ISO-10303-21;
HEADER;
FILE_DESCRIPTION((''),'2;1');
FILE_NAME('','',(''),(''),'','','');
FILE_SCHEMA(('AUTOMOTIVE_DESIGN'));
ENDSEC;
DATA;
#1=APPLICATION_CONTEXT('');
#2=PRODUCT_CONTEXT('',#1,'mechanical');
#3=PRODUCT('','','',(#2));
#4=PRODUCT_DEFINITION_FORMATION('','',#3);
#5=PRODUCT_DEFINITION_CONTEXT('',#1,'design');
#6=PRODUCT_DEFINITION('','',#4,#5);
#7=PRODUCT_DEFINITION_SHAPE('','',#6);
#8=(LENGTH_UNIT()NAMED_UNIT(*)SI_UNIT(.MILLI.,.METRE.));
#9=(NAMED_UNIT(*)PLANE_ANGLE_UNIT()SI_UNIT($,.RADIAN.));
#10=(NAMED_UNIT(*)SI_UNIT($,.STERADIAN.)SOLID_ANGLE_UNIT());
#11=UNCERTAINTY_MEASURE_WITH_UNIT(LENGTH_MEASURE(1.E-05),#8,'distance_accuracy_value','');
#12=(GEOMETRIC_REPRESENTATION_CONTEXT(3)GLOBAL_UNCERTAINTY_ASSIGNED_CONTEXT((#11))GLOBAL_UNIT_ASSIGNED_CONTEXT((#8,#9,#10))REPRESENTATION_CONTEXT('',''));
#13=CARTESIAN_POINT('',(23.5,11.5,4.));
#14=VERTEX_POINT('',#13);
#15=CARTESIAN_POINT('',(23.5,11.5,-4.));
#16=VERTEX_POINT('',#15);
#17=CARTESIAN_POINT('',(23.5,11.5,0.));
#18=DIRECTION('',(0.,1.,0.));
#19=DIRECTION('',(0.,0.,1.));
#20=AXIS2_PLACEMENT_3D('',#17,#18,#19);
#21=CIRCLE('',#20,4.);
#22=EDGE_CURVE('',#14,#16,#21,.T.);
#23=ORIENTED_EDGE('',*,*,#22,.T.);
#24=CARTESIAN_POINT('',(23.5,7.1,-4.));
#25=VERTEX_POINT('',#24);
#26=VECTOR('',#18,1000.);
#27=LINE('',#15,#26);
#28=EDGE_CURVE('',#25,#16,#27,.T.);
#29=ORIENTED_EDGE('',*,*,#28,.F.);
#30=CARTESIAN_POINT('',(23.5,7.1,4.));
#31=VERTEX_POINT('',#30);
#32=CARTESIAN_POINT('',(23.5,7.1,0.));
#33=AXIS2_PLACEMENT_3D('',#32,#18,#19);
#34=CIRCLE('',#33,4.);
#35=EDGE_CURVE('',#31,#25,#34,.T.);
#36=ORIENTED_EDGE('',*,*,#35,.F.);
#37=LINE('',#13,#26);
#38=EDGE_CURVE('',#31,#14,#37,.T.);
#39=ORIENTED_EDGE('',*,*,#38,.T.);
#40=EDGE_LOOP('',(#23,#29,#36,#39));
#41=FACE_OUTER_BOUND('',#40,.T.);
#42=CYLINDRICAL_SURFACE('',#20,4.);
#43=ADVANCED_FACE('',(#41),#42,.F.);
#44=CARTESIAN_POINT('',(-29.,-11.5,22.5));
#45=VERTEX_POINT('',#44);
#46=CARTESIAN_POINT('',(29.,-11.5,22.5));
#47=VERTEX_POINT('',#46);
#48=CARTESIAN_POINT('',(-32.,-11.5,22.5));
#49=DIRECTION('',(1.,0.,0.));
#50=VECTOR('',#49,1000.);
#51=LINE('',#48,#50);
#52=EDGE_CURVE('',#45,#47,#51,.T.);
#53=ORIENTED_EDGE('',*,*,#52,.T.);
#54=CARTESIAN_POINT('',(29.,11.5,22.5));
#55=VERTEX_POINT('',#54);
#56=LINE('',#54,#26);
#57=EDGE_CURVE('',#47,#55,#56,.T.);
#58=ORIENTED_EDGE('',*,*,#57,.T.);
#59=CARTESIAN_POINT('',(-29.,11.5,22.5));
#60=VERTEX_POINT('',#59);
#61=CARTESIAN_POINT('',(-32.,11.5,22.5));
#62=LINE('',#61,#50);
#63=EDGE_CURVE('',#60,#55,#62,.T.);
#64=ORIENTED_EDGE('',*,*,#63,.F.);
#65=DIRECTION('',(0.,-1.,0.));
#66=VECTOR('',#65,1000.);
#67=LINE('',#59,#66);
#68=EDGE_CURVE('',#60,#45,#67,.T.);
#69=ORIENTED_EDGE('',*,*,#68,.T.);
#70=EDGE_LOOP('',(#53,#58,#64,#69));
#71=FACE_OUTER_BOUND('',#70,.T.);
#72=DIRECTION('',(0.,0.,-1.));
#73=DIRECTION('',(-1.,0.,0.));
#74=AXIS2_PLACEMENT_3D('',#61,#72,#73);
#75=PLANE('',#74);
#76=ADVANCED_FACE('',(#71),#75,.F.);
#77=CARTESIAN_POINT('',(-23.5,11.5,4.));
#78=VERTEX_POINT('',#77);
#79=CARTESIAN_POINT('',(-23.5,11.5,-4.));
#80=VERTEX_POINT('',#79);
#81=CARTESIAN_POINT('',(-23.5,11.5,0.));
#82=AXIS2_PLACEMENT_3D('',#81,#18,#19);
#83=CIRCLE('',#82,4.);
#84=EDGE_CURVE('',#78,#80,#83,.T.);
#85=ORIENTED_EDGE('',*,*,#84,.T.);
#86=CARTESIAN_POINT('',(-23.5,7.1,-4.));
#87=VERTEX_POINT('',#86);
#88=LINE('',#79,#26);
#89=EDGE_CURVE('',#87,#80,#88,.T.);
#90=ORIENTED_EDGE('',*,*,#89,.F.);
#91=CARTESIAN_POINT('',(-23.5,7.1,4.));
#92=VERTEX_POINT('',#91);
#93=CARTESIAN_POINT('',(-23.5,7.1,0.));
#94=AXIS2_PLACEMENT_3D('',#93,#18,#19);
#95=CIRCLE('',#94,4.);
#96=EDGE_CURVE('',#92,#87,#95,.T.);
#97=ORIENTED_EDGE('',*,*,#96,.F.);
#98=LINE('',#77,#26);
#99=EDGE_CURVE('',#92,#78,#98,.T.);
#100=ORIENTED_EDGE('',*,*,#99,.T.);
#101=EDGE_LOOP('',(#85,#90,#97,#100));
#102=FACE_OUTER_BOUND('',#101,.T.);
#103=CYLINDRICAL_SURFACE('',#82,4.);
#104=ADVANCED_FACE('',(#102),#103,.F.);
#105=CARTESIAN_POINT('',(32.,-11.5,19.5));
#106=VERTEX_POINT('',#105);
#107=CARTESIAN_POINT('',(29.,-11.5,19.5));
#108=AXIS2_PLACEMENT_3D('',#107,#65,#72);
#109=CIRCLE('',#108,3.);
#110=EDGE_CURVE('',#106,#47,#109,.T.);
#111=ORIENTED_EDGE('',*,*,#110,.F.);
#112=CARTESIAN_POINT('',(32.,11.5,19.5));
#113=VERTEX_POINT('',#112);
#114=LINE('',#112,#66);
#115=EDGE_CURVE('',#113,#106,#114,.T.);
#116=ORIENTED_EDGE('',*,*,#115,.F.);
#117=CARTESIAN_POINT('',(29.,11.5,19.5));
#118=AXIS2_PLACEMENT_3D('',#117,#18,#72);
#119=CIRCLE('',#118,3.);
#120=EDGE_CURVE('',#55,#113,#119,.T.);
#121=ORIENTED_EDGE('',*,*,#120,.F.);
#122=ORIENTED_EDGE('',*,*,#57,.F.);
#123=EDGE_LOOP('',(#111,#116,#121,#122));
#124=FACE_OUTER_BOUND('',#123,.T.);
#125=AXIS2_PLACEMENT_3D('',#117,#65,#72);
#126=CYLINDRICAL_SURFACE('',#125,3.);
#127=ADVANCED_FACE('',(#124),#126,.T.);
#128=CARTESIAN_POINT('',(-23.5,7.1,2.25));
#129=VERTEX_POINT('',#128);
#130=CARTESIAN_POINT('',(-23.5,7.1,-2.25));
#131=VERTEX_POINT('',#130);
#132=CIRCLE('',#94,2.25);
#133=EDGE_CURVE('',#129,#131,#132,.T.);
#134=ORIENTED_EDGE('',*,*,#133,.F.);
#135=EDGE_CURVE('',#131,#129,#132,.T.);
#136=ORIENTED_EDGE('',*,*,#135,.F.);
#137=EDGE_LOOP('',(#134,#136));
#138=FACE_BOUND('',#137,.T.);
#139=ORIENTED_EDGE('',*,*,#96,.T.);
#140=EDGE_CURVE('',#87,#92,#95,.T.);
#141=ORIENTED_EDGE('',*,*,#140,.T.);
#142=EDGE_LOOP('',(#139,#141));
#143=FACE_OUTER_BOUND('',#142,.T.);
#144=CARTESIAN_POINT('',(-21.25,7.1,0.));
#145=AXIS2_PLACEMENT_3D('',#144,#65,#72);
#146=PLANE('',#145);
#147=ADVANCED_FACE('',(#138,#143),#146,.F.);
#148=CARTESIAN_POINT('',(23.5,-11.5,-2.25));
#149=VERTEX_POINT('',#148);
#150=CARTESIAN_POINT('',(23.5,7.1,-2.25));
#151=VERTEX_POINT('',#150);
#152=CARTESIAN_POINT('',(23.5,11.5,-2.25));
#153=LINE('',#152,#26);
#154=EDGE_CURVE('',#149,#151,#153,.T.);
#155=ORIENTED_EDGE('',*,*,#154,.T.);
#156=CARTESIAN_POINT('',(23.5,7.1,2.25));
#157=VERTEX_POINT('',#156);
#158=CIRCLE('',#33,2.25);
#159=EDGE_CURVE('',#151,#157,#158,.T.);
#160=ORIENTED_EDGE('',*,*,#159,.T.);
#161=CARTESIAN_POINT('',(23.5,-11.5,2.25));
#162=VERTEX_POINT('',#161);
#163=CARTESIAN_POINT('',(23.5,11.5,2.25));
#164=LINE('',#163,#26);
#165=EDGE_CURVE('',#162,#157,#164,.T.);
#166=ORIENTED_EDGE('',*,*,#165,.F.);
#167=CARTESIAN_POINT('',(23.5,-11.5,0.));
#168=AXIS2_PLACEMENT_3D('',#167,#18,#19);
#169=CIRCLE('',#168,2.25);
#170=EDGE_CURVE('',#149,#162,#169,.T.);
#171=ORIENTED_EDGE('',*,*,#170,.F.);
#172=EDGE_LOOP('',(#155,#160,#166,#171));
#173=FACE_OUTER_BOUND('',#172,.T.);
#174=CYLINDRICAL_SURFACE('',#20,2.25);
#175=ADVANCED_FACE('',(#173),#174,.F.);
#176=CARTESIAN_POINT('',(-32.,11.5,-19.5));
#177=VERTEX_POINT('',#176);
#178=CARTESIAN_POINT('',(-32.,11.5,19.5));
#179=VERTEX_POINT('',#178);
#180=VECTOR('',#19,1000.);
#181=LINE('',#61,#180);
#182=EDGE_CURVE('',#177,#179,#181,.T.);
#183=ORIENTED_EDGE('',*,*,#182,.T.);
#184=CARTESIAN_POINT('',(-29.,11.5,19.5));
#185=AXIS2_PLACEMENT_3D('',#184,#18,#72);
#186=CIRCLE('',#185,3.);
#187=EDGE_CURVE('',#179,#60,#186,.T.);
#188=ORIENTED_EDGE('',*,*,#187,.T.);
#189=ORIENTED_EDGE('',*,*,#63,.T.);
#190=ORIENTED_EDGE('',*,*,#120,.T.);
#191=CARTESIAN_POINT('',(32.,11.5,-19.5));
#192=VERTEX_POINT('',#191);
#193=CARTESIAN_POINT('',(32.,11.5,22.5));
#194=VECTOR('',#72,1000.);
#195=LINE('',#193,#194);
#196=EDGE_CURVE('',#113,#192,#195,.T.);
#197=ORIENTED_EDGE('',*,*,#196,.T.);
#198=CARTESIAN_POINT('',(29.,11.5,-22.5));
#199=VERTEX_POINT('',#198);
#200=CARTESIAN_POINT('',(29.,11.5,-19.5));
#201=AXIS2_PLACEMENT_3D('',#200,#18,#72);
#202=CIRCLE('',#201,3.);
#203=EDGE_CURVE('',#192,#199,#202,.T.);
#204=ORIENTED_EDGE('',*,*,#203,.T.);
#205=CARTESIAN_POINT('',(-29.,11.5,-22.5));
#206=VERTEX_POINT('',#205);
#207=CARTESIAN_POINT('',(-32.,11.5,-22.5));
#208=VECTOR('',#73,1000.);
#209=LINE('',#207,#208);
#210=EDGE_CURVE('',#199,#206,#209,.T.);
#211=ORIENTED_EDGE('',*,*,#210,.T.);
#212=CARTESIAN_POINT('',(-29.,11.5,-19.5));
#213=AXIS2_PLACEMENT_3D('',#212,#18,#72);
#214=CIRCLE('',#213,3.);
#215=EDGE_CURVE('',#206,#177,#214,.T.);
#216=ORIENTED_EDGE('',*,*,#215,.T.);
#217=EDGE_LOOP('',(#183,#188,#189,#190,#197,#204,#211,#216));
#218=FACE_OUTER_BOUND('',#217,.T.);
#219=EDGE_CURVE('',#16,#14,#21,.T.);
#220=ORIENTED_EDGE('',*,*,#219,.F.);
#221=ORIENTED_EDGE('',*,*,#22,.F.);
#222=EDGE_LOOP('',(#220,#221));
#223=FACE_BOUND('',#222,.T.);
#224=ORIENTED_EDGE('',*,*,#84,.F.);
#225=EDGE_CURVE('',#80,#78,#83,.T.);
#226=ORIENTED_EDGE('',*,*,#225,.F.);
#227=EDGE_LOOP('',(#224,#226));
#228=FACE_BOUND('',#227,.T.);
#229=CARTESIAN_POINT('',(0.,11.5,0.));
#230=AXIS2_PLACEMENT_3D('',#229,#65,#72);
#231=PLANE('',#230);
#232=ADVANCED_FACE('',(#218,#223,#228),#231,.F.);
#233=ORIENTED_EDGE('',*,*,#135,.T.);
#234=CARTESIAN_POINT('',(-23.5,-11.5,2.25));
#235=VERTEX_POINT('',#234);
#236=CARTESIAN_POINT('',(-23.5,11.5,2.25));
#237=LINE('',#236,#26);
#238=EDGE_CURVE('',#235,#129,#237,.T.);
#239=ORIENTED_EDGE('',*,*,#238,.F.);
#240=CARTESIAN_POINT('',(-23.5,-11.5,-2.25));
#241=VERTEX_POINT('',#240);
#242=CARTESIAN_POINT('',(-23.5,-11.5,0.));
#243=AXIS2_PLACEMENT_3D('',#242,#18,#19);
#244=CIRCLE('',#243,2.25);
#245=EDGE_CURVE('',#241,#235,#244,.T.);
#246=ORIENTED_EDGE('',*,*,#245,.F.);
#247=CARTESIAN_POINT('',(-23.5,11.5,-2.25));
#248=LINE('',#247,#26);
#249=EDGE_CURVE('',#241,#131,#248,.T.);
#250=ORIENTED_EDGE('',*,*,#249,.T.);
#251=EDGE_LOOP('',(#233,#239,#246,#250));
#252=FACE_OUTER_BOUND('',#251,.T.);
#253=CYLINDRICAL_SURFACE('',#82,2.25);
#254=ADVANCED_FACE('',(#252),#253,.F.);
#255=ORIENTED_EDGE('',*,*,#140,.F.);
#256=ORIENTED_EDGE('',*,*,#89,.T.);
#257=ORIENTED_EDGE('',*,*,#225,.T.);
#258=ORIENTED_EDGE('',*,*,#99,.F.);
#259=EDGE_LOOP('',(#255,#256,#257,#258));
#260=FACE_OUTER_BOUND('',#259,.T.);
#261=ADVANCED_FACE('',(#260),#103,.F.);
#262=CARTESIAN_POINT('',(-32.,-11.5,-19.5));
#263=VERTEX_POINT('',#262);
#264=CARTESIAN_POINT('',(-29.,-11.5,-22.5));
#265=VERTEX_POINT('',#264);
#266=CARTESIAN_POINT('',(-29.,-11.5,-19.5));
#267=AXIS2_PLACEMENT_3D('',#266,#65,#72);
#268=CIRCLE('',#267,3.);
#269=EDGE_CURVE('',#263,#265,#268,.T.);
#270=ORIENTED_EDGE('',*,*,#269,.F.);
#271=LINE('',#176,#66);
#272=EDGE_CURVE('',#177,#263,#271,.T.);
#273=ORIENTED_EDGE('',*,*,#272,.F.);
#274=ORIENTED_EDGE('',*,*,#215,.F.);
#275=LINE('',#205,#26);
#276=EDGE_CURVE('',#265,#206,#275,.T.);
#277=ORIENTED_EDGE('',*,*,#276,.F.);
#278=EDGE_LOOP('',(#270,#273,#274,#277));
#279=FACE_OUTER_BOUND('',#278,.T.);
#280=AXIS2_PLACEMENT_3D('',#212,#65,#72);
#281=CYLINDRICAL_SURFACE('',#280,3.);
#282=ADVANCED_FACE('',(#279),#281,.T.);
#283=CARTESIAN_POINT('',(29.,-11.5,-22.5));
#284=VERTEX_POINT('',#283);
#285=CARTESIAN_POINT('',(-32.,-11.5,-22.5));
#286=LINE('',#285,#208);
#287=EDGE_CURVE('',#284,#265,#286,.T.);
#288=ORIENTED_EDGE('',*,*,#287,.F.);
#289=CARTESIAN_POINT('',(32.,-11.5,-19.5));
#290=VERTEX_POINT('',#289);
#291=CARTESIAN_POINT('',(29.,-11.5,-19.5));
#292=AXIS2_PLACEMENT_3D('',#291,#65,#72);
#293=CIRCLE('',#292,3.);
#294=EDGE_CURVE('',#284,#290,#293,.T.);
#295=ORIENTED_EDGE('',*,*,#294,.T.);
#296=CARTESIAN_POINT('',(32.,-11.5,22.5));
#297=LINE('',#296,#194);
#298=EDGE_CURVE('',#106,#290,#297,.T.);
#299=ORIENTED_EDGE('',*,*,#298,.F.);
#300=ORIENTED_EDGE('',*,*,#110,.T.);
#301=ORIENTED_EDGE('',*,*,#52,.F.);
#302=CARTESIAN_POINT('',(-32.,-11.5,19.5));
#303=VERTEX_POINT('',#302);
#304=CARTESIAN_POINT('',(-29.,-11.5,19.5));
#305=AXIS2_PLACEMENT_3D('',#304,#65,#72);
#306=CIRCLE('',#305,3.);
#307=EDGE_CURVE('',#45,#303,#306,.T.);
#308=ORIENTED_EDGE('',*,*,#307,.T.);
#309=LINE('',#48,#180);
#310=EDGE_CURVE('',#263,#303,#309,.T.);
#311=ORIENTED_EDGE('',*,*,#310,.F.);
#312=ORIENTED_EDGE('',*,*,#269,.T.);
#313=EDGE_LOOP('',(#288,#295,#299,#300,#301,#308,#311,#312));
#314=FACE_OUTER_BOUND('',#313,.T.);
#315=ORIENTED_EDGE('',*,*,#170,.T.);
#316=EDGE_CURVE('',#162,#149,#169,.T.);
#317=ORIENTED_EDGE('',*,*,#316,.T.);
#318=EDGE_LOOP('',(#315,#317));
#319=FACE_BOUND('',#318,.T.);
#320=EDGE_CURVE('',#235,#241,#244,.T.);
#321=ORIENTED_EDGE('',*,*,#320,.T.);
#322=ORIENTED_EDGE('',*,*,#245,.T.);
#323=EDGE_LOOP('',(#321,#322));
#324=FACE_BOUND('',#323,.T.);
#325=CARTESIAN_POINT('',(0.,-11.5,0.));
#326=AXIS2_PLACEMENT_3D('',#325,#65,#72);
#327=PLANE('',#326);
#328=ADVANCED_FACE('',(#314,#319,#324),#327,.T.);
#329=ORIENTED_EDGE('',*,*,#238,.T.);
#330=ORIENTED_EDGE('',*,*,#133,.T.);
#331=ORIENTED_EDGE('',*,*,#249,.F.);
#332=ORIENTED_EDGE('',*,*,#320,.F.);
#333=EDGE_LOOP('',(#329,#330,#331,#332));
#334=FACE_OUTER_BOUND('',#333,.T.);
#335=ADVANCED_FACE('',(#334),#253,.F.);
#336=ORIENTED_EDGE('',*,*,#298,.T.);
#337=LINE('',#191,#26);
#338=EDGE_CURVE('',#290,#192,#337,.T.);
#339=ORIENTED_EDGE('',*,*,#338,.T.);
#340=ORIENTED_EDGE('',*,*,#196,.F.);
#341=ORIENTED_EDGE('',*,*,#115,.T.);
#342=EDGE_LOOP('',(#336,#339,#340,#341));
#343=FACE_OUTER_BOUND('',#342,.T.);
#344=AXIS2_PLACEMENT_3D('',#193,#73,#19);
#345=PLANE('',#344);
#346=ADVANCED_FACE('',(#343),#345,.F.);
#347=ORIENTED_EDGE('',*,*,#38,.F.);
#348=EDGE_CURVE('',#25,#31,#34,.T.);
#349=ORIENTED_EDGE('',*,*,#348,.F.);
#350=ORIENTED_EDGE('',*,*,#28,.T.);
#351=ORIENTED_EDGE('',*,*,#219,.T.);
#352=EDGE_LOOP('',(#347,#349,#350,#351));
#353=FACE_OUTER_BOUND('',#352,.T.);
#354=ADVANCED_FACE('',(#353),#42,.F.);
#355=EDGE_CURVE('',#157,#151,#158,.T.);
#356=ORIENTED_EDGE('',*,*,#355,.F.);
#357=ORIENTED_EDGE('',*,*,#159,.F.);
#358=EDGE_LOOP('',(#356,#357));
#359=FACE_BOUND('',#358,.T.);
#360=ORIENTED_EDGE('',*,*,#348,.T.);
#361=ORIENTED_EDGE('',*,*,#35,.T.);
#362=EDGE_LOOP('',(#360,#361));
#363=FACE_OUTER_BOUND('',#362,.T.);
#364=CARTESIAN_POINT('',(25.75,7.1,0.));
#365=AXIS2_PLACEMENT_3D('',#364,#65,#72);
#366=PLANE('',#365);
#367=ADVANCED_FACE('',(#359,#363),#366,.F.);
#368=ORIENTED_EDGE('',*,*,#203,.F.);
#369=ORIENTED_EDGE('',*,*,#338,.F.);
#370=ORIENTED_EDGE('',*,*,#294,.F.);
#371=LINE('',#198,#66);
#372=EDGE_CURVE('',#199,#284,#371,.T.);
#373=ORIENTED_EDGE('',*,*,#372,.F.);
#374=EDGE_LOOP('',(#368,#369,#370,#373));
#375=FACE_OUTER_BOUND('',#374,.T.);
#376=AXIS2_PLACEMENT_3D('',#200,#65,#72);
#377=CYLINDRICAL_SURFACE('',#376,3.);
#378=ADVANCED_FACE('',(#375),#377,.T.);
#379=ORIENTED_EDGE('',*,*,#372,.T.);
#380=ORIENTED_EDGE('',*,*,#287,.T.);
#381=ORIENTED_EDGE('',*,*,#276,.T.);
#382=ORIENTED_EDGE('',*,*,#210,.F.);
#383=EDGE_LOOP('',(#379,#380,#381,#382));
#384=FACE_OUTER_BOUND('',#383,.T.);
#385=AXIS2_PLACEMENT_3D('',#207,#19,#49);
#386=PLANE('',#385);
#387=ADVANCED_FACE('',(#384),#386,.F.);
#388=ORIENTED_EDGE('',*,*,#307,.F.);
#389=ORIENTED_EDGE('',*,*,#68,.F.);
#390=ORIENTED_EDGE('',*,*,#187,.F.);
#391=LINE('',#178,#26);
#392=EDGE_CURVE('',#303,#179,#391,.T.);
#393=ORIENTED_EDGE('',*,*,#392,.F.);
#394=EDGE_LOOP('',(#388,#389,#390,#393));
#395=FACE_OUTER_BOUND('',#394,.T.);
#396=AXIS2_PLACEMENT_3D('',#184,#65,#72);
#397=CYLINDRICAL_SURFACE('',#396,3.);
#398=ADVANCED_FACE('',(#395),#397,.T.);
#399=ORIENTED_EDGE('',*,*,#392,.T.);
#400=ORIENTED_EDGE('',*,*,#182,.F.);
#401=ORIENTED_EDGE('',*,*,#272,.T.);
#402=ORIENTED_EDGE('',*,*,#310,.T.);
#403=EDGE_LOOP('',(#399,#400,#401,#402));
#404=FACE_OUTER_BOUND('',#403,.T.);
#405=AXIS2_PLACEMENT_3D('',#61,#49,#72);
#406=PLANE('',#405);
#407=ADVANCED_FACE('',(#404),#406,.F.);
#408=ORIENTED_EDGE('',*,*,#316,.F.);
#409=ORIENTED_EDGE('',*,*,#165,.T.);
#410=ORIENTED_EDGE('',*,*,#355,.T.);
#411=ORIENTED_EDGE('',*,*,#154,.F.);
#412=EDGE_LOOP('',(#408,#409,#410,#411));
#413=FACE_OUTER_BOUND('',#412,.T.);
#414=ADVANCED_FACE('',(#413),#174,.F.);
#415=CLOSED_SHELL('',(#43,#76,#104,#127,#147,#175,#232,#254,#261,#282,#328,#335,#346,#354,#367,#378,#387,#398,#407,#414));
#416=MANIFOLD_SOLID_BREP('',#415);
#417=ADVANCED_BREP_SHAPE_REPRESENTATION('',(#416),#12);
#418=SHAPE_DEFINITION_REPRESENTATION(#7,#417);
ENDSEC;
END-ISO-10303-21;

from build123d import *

# Parameters (mm, degrees)
SKETCH_1_W                   = 64
SKETCH_1_H                   = 45
EXTRUDE_1_DEPTH              = 11.5
HOLE_WIZARD_M4_1_D           = 4.5
HOLE_WIZARD_M4_1_CBORE_D     = 8
HOLE_WIZARD_M4_1_CBORE_DEPTH = 4.4
FILLET_1_R                   = 3


with BuildPart() as part:
    # 草图1 → 凸台-拉伸1 (new, symmetric)
    with BuildSketch(Plane(origin=(0, 0, 0), x_dir=(1, 0, 0), z_dir=(0, 1, 0))):
        Rectangle(SKETCH_1_W, SKETCH_1_H)
    extrude(amount=EXTRUDE_1_DEPTH, both=True)

    # M4 六角凹头螺钉的柱形沉头孔1 (through all)
    with Locations(Plane(origin=(0, 11.5, 0), x_dir=(1, 0, 0), z_dir=(0, 1, 0))):
        with Locations((-23.5, 0), (23.5, 0)):
            CounterBoreHole(HOLE_WIZARD_M4_1_D / 2, HOLE_WIZARD_M4_1_CBORE_D / 2, HOLE_WIZARD_M4_1_CBORE_DEPTH)

    # 圆角1
    fillet_1_edges = [part.edges().sort_by_distance(p)[0] for p in [
        (32, 0, 22.5),
        (-32, 0, 22.5),
        (-32, 0, -22.5),
        (32, 0, -22.5),
    ]]
    fillet(fillet_1_edges, radius=FILLET_1_R)


solid = part.part
